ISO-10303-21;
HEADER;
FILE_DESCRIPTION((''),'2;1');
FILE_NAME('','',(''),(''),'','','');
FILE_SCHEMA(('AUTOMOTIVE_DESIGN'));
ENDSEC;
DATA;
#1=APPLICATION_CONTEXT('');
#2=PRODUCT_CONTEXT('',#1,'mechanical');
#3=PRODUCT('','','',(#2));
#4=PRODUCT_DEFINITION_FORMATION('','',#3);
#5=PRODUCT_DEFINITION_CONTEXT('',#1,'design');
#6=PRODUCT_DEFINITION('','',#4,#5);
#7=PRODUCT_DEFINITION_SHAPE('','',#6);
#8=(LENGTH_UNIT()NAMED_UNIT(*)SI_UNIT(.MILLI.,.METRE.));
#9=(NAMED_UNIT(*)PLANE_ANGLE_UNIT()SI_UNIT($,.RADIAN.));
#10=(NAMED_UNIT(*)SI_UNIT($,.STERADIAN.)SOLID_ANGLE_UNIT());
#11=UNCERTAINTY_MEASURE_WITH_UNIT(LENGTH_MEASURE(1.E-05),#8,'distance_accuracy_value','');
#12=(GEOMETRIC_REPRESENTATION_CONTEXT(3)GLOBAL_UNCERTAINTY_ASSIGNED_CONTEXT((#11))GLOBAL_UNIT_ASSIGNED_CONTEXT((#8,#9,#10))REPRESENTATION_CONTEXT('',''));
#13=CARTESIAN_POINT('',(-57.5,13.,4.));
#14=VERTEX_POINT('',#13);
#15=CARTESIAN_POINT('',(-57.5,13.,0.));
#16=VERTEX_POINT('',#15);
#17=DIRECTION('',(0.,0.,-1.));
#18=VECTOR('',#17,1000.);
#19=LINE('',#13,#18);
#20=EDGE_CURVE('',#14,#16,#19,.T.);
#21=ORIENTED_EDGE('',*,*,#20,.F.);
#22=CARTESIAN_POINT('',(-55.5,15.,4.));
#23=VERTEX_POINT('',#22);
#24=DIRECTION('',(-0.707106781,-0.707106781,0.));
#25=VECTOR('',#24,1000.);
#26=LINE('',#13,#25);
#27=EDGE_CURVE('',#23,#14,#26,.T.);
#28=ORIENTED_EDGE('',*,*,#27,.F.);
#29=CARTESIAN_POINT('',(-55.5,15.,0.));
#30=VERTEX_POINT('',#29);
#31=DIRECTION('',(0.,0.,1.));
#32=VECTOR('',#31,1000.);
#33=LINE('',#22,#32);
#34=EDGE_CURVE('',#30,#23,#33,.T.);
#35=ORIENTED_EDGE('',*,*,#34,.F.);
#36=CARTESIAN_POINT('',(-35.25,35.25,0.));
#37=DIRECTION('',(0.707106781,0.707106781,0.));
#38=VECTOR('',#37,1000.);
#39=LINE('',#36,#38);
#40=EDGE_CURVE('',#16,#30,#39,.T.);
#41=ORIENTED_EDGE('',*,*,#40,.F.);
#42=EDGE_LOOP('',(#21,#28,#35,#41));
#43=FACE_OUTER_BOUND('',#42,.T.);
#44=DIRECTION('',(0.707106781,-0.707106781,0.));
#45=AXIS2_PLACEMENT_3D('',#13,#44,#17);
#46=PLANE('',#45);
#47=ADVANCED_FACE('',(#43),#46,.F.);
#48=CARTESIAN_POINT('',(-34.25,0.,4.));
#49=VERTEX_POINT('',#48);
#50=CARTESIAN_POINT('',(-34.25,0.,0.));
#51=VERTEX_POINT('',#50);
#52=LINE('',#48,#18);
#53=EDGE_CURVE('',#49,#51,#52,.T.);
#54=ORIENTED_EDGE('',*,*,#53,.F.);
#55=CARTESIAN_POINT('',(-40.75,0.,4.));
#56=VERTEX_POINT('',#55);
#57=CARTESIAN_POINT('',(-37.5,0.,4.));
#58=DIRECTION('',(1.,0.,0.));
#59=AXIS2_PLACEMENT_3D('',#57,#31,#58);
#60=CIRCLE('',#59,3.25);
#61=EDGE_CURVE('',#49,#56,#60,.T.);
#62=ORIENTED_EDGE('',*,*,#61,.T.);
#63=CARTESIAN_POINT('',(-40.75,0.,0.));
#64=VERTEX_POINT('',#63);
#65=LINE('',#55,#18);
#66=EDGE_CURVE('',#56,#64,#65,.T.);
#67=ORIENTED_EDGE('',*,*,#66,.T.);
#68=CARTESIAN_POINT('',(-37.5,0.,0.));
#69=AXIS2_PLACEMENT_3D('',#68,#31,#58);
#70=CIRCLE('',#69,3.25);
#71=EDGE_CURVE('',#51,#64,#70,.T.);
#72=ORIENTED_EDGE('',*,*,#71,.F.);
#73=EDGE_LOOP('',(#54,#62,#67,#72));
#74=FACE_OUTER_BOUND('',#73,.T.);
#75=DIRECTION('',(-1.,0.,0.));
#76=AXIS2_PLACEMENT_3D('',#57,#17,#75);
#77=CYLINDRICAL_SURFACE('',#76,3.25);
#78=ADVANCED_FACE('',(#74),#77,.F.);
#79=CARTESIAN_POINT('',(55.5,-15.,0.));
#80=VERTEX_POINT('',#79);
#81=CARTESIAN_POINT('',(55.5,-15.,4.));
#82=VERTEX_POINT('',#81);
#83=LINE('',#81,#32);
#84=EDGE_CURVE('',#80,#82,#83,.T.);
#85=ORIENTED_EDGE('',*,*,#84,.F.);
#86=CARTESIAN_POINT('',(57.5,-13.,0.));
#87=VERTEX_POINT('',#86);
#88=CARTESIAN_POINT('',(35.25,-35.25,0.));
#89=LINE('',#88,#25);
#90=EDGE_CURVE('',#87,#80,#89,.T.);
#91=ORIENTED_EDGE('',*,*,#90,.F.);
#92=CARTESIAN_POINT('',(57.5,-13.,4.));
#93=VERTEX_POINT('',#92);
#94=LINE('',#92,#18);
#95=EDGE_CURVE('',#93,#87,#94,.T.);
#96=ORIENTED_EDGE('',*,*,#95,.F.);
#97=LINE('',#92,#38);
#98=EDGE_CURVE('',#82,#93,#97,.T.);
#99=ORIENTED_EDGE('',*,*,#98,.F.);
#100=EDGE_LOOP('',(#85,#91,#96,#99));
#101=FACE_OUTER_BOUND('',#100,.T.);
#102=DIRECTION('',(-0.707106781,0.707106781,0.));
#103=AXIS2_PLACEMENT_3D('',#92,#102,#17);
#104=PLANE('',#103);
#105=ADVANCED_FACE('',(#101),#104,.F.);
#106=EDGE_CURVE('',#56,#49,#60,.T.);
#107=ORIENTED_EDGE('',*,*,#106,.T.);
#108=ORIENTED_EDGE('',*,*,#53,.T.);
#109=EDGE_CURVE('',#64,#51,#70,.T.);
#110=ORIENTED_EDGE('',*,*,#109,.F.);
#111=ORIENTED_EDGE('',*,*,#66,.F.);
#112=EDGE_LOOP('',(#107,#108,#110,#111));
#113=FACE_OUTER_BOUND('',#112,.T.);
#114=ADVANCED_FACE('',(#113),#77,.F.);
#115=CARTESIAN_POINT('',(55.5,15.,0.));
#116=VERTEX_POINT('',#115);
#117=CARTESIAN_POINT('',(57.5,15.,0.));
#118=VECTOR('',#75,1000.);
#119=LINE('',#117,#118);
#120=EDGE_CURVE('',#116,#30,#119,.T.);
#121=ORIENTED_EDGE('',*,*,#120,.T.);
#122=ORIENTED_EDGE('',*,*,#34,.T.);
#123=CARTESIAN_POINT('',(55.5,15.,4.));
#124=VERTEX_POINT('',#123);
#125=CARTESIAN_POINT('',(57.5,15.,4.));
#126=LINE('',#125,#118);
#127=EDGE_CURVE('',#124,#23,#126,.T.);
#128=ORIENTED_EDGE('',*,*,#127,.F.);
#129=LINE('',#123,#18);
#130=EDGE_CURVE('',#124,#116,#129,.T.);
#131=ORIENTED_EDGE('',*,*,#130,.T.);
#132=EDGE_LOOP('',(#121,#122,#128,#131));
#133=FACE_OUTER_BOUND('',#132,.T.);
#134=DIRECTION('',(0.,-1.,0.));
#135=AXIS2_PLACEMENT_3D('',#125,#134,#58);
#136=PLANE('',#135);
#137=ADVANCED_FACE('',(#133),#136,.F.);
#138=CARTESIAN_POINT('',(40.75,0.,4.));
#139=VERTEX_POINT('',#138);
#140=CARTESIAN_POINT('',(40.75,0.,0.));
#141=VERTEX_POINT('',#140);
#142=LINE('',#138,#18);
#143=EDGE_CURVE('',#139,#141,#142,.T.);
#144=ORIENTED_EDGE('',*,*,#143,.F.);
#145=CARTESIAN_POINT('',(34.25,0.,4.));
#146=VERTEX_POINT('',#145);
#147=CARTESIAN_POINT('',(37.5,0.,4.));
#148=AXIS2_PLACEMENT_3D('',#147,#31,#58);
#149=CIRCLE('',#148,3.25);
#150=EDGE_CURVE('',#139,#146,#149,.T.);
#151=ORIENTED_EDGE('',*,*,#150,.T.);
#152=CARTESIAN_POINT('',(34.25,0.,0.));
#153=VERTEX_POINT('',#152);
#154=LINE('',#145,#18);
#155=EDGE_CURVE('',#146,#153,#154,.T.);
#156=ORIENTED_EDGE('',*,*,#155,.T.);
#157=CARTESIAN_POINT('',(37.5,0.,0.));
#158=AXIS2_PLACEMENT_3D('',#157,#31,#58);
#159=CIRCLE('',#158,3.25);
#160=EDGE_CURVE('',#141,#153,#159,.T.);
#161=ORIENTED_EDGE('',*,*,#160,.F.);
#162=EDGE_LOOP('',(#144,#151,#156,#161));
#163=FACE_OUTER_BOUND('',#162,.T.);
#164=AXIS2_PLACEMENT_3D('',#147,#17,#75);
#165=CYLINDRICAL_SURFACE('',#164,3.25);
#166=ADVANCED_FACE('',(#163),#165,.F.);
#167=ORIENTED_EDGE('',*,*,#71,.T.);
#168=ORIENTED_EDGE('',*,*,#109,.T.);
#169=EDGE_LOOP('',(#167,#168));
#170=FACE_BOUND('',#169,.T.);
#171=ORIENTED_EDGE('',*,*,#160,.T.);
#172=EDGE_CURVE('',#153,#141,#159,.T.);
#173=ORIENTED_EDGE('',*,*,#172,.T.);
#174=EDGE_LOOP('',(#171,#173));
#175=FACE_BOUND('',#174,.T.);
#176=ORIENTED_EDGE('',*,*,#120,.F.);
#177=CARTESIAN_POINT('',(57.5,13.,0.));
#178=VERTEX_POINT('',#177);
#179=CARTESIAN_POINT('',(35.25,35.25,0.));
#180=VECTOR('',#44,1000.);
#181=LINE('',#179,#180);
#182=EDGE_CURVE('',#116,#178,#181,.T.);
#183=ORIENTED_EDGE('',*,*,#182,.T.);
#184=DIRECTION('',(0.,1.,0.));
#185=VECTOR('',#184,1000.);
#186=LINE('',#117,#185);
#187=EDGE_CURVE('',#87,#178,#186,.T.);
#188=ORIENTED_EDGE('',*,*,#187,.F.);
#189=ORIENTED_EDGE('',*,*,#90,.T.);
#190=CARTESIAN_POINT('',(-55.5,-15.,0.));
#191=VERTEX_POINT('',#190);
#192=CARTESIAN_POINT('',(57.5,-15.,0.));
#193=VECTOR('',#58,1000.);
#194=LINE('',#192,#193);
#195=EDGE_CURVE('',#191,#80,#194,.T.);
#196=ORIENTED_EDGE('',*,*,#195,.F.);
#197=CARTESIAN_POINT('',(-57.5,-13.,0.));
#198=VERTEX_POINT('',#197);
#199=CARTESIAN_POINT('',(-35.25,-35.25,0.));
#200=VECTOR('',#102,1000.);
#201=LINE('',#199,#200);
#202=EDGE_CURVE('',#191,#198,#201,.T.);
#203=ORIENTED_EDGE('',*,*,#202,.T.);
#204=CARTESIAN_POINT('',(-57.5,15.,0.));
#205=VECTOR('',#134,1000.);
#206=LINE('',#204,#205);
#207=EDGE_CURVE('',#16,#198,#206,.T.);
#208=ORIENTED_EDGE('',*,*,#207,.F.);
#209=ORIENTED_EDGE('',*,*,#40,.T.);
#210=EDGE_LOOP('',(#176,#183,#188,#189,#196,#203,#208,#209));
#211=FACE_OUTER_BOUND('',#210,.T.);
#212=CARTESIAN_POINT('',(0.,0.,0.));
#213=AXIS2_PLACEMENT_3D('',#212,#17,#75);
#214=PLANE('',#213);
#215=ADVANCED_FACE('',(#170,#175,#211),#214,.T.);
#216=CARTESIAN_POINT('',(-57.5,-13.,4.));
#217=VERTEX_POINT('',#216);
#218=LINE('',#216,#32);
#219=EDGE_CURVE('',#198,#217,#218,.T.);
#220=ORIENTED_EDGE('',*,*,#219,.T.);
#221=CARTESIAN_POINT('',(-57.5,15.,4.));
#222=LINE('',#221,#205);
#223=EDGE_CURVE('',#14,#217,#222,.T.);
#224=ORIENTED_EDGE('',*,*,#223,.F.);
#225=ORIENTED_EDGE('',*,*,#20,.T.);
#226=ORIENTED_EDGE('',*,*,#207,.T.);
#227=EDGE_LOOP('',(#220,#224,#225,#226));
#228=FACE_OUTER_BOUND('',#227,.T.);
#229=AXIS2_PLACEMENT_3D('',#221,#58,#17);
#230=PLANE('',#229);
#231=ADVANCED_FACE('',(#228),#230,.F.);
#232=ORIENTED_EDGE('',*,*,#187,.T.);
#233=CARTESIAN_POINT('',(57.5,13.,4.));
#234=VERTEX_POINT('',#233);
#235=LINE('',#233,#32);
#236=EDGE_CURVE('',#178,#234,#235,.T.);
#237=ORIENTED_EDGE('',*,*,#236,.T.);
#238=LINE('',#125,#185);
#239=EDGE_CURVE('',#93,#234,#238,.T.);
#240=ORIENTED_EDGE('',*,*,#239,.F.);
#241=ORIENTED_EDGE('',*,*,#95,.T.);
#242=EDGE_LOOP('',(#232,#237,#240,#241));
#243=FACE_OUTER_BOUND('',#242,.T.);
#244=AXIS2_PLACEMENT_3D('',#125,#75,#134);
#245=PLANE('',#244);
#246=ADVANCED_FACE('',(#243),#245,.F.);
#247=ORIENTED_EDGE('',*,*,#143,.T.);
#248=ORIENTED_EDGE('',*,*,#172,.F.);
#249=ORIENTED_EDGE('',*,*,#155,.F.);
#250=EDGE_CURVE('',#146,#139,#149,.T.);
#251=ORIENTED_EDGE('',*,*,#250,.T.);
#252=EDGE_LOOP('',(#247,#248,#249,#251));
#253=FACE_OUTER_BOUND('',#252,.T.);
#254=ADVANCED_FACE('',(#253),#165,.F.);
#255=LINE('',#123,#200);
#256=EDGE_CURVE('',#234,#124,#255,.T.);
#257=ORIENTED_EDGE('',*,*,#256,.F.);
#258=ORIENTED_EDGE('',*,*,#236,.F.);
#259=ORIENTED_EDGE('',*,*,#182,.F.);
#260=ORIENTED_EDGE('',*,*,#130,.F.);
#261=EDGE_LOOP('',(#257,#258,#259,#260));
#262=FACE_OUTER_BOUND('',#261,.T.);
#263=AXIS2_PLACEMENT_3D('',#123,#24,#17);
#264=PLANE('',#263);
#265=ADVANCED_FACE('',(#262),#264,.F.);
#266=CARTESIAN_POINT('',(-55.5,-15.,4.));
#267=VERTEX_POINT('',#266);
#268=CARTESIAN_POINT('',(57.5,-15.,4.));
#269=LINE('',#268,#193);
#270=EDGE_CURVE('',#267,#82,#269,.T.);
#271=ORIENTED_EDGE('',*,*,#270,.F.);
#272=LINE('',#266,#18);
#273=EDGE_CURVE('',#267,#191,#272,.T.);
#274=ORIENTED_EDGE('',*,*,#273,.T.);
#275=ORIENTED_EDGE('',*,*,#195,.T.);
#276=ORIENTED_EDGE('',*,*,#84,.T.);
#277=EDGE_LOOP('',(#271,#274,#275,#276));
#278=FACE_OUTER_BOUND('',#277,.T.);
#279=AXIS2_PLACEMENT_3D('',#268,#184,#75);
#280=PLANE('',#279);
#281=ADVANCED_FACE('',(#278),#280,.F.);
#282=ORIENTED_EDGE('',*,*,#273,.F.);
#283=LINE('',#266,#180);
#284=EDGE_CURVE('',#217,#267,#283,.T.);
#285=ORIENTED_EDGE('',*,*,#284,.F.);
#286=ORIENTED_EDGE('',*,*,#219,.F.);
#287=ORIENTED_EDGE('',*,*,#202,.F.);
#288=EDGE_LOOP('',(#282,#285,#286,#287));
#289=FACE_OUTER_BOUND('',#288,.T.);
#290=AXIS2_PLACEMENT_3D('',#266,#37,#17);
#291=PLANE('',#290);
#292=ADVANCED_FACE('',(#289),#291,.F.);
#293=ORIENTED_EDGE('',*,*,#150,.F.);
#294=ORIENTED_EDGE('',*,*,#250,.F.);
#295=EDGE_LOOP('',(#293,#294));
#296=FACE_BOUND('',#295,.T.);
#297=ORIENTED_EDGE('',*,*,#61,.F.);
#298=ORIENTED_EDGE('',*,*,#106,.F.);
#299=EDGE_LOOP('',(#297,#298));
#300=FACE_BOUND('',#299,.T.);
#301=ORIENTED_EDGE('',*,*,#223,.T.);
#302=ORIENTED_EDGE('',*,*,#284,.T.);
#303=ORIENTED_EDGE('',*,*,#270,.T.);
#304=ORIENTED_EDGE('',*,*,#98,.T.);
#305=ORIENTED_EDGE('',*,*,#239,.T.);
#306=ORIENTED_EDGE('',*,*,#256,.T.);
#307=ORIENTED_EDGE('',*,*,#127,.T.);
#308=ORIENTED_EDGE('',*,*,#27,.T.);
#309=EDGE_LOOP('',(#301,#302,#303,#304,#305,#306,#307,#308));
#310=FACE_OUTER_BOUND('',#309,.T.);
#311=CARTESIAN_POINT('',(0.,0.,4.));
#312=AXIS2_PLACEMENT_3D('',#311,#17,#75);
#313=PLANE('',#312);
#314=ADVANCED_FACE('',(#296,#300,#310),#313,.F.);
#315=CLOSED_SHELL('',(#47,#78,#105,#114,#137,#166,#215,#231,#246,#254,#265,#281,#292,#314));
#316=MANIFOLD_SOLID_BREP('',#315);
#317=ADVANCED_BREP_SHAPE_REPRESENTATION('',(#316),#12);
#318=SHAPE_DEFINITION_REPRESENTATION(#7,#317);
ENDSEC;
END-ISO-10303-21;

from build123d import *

# Parameters (mm, degrees)
SKETCH1_W           = 115
SKETCH1_H           = 30
SKETCH1_R           = 3.25
BOSS_EXTRUDE1_DEPTH = 4
CHAMFER1_SIZE       = 2


with BuildPart() as part:
    # Sketch1 → Boss-Extrude1 (new body)
    with BuildSketch(Plane.XY):
        Rectangle(SKETCH1_W, SKETCH1_H)
        with Locations((-37.5, 0)):
            Circle(SKETCH1_R, mode=Mode.SUBTRACT)
        with Locations((37.5, 0)):
            Circle(SKETCH1_R, mode=Mode.SUBTRACT)
    extrude(amount=BOSS_EXTRUDE1_DEPTH)

    # Chamfer1
    chamfer1_edges = [part.edges().sort_by_distance(p)[0] for p in [
        (-57.5, 15, 2),
        (57.5, 15, 2),
        (57.5, -15, 2),
        (-57.5, -15, 2),
    ]]
    chamfer(chamfer1_edges, length=CHAMFER1_SIZE)


solid = part.part
